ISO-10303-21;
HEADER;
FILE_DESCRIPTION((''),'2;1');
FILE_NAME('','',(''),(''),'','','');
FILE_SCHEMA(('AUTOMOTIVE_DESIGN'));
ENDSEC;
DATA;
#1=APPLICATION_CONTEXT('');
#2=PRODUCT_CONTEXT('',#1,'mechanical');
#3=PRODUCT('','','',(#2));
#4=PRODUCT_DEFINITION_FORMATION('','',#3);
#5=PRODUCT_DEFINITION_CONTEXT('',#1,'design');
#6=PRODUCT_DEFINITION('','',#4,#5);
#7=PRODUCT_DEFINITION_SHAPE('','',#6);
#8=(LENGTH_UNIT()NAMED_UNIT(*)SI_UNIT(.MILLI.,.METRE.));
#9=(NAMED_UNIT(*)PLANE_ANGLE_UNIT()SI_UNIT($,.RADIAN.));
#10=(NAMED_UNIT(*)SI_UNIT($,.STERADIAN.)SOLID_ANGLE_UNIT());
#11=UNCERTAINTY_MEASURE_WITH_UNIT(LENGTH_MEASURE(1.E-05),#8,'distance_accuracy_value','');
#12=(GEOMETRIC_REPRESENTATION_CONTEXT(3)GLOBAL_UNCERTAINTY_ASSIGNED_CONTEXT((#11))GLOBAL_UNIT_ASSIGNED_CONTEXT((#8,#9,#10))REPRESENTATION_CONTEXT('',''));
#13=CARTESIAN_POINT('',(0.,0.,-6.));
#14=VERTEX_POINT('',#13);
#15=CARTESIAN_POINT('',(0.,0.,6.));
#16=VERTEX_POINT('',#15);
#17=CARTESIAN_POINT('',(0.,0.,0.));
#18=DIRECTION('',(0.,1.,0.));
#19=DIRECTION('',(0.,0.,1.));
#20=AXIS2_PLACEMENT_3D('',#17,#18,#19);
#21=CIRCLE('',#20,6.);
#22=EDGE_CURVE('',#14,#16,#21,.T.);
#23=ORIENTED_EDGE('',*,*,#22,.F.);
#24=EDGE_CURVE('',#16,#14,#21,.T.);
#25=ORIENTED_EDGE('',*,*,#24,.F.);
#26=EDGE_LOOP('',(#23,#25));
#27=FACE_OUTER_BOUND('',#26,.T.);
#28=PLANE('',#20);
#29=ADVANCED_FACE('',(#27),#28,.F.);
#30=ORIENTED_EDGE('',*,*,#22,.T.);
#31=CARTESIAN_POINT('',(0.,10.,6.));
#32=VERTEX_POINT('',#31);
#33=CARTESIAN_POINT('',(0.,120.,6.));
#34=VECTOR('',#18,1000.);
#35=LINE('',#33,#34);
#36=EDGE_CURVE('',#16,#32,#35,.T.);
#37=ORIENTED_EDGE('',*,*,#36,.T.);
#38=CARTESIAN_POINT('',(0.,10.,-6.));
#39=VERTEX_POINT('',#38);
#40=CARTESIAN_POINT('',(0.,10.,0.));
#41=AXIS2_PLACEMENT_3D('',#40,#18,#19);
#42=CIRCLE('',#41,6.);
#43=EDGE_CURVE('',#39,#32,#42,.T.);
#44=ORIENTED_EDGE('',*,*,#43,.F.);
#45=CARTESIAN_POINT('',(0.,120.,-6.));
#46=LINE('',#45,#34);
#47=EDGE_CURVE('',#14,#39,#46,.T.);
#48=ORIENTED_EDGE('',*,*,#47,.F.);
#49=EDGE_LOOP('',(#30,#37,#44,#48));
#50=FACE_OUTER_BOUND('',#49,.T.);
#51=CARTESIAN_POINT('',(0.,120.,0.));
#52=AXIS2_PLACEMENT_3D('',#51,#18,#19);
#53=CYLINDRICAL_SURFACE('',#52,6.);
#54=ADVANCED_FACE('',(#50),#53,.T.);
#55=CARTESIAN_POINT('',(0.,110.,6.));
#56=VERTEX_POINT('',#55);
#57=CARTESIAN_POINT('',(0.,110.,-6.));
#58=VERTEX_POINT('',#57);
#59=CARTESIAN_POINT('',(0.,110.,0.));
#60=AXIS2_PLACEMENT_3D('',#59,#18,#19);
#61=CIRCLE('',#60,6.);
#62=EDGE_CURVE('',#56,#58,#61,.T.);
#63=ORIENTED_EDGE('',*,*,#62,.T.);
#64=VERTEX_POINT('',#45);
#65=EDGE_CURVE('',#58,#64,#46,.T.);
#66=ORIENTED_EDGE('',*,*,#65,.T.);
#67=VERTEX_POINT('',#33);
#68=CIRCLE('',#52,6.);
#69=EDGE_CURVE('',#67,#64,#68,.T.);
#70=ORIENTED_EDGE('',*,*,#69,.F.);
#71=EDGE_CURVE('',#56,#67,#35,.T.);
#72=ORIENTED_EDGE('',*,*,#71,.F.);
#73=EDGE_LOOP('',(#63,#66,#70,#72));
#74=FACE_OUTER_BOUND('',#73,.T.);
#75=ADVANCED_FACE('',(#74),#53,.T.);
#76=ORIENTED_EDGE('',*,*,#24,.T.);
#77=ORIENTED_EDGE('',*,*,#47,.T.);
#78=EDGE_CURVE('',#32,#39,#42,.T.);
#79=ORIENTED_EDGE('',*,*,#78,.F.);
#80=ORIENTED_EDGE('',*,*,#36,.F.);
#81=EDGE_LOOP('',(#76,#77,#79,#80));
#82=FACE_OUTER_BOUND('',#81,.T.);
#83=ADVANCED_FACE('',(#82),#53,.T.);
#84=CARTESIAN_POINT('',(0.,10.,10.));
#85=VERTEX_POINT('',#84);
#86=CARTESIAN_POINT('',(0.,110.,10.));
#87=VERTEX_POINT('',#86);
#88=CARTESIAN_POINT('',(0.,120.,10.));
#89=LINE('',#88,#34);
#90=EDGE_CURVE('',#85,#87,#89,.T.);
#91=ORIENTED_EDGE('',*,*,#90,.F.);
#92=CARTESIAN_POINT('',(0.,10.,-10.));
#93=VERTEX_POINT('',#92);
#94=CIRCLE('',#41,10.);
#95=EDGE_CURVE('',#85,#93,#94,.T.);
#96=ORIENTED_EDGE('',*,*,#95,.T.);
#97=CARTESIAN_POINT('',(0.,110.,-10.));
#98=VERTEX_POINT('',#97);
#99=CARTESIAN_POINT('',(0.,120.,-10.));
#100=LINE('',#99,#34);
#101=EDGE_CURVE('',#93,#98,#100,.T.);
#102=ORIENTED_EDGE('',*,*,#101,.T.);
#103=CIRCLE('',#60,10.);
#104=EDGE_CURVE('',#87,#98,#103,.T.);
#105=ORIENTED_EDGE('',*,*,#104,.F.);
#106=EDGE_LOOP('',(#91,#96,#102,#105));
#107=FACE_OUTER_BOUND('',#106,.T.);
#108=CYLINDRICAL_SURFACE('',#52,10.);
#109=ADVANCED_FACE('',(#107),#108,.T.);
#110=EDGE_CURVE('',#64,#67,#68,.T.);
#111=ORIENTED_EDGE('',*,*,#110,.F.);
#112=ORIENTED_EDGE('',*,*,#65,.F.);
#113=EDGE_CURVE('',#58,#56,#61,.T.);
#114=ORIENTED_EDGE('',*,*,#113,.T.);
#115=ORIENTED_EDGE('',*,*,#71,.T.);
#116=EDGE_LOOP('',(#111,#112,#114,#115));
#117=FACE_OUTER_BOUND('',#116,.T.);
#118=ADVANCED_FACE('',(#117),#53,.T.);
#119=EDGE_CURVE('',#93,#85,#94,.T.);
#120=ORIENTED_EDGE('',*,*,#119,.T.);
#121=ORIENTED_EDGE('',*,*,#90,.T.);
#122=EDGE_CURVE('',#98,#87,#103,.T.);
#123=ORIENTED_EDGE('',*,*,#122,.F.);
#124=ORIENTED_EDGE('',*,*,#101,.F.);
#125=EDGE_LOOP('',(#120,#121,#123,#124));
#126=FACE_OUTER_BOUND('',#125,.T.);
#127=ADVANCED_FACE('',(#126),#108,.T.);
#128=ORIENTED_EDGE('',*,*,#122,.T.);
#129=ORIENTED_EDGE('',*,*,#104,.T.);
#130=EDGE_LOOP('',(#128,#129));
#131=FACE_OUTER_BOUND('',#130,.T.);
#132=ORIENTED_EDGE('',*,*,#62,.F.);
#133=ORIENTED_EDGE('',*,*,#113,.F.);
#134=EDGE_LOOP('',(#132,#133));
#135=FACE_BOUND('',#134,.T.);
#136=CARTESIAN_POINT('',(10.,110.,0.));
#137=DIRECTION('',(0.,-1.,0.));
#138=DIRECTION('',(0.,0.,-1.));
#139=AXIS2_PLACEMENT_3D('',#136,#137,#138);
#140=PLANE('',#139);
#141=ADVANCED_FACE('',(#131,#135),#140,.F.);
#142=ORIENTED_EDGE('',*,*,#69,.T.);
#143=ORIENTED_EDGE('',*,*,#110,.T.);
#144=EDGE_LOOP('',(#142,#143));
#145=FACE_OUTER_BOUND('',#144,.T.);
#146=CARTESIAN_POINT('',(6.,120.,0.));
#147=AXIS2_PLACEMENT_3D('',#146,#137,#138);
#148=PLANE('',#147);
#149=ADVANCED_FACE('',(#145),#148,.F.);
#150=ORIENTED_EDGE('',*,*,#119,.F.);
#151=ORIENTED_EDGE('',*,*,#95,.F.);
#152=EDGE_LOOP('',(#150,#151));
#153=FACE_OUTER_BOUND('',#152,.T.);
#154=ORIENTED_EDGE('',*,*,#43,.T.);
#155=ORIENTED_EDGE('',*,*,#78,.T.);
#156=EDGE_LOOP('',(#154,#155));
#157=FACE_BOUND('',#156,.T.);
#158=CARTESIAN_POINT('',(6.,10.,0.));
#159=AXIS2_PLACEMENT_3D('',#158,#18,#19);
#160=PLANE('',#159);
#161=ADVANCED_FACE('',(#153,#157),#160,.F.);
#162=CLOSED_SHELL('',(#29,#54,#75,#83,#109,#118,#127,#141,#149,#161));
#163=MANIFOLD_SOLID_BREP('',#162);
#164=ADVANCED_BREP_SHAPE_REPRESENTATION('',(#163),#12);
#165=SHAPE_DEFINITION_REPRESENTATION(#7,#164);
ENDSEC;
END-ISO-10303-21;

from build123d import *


with BuildPart() as part:
    # Shaft Profile Sketch → Stepped Shaft Ø20 Journals Ø12 (revolve)
    with BuildSketch(Plane.XY, mode=Mode.PRIVATE) as stepped_shaft_20_journals_12_sk:
        Polygon((0, 0), (6, 0), (6, 10), (10, 10), (10, 110), (6, 110), (6, 120), (0, 120), align=None)
    revolve(stepped_shaft_20_journals_12_sk.sketch.rotate(Axis((0, 120, 0), (0, -1, 0)), 90), axis=Axis((0, 120, 0), (0, -1, 0)))


solid = part.part
